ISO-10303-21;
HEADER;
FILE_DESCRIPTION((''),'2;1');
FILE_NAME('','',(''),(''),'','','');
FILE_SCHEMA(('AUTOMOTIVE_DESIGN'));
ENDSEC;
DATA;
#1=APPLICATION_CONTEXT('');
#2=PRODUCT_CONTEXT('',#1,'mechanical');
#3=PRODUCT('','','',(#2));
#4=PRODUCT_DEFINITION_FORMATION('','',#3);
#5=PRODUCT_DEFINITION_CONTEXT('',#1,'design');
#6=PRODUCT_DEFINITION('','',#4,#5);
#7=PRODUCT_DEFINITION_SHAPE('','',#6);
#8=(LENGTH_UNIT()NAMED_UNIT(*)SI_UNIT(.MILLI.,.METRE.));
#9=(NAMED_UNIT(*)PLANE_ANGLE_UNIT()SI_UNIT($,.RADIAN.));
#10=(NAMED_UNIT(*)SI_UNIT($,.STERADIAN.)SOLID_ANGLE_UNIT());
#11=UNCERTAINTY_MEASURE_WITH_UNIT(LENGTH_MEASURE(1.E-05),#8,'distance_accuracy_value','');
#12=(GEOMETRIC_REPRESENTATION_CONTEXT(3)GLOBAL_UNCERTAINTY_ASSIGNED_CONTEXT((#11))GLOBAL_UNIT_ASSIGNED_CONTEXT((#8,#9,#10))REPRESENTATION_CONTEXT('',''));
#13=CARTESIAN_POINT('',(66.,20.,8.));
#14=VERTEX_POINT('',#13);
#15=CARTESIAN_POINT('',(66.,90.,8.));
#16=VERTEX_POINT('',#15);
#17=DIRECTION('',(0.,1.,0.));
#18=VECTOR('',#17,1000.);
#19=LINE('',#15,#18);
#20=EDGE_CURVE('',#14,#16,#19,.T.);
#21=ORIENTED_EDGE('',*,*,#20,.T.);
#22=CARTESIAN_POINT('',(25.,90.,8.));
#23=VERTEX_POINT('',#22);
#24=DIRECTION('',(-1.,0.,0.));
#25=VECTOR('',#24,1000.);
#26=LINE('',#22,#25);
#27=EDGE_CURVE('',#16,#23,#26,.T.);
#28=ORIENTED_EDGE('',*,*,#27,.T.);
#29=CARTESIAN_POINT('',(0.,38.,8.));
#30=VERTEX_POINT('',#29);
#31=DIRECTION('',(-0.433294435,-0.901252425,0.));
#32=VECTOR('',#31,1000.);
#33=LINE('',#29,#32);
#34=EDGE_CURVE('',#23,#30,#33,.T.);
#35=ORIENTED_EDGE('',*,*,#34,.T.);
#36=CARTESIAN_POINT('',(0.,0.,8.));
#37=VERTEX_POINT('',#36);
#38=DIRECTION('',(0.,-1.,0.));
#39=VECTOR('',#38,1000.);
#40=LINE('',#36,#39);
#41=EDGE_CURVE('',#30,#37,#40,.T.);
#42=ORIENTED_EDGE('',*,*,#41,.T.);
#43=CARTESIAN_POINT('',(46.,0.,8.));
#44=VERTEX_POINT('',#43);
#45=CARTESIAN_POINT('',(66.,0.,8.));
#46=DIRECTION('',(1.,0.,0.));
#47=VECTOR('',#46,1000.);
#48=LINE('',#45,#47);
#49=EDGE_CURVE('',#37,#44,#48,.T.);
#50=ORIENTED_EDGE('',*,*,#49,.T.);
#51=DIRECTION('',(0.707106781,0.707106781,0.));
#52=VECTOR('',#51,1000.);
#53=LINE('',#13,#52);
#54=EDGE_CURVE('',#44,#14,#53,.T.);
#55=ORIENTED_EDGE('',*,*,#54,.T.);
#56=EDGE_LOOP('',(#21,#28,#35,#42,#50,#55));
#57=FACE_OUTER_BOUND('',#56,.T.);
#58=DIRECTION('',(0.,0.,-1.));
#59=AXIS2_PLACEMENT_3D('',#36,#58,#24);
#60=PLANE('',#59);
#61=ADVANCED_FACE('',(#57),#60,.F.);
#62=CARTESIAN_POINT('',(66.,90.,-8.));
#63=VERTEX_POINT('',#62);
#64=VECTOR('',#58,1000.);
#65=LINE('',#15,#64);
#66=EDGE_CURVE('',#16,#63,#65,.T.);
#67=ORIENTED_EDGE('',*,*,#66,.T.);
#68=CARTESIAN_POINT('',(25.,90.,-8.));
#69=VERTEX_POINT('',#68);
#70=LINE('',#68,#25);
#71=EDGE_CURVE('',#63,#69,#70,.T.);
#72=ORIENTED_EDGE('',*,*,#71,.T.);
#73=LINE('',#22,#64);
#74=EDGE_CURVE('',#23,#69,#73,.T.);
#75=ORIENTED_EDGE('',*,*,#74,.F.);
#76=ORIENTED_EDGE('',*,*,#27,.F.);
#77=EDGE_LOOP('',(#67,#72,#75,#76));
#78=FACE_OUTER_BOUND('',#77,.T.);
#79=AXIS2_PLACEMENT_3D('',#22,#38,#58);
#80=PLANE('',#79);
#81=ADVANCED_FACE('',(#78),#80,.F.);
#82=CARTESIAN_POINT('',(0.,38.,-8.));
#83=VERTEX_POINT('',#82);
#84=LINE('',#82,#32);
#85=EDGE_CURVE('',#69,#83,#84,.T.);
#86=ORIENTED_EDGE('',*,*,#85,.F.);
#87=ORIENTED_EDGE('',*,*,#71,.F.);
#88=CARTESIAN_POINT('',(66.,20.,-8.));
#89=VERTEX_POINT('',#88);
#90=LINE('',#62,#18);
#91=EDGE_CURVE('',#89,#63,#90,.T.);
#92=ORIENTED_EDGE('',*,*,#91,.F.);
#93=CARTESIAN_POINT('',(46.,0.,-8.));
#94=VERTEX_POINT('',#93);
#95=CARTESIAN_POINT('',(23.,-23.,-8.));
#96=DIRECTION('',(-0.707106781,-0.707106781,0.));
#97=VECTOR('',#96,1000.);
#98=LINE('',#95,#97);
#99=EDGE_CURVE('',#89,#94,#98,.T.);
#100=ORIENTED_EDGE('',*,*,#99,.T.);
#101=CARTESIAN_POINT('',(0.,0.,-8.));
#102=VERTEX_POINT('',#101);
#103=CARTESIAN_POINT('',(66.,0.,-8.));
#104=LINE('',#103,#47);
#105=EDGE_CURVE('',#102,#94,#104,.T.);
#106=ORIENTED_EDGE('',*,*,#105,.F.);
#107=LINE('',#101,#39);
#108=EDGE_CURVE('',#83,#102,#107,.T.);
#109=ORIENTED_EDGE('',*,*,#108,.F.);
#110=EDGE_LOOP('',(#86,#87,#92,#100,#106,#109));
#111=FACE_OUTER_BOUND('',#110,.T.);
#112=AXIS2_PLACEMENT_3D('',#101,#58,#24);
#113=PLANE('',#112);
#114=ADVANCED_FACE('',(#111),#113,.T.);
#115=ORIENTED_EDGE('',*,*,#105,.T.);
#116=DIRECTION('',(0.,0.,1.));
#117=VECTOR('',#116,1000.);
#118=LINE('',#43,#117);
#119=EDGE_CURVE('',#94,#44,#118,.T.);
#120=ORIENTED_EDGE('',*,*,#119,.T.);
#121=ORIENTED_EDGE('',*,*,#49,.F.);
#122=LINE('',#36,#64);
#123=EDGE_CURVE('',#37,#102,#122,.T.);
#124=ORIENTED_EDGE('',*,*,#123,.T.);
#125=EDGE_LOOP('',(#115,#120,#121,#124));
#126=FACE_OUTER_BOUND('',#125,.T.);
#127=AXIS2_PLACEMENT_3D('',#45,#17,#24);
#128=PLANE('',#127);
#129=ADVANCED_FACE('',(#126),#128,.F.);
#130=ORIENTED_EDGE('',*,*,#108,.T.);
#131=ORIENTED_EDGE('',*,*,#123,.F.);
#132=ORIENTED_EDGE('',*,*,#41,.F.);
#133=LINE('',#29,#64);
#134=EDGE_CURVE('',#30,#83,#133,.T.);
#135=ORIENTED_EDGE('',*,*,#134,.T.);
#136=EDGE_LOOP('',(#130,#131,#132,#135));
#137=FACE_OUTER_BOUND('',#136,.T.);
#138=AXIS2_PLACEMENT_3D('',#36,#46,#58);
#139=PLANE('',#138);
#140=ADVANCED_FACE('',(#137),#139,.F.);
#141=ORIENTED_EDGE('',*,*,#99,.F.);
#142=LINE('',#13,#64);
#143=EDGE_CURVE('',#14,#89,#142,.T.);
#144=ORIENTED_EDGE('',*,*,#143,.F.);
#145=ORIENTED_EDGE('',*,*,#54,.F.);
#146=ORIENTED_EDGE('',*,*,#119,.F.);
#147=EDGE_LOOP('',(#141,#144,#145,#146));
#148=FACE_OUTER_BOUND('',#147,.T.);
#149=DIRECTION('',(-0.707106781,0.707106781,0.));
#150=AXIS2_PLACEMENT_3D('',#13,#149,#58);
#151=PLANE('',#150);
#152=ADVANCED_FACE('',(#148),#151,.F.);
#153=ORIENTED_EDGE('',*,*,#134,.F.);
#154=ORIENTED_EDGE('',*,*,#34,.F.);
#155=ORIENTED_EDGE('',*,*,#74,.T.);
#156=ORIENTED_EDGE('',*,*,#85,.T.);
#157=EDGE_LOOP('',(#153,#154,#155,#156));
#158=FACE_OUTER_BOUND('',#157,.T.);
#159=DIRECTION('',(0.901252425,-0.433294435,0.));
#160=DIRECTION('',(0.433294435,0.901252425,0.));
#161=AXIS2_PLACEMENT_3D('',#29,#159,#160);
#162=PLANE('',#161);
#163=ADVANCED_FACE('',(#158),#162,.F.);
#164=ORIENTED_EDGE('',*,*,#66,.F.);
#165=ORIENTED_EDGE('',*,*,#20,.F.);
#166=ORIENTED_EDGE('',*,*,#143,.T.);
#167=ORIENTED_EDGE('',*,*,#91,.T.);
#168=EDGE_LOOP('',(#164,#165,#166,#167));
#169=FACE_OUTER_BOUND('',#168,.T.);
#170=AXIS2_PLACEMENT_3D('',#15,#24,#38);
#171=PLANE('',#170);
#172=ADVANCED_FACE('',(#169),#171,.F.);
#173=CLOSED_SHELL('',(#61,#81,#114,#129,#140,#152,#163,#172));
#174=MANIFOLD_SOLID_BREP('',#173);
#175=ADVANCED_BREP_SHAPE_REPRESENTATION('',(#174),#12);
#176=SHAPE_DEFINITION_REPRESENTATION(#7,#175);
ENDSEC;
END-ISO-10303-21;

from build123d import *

# Parameters (mm, degrees)
EXTRUDE_1_DEPTH = 8
CHAMFER_1_SIZE  = 20


with BuildPart() as part:
    # 草图2 → 凸台-拉伸1 (new, symmetric)
    with BuildSketch(Plane.XY):
        Polygon((25, 90), (66, 90), (66, 0), (0, 0), (0, 38), align=None)
    extrude(amount=EXTRUDE_1_DEPTH, both=True)

    # 倒角1
    chamfer_1_edges = [part.edges().sort_by_distance(p)[0] for p in [
        (66, 0, 0),
    ]]
    chamfer(chamfer_1_edges, length=CHAMFER_1_SIZE)


solid = part.part
